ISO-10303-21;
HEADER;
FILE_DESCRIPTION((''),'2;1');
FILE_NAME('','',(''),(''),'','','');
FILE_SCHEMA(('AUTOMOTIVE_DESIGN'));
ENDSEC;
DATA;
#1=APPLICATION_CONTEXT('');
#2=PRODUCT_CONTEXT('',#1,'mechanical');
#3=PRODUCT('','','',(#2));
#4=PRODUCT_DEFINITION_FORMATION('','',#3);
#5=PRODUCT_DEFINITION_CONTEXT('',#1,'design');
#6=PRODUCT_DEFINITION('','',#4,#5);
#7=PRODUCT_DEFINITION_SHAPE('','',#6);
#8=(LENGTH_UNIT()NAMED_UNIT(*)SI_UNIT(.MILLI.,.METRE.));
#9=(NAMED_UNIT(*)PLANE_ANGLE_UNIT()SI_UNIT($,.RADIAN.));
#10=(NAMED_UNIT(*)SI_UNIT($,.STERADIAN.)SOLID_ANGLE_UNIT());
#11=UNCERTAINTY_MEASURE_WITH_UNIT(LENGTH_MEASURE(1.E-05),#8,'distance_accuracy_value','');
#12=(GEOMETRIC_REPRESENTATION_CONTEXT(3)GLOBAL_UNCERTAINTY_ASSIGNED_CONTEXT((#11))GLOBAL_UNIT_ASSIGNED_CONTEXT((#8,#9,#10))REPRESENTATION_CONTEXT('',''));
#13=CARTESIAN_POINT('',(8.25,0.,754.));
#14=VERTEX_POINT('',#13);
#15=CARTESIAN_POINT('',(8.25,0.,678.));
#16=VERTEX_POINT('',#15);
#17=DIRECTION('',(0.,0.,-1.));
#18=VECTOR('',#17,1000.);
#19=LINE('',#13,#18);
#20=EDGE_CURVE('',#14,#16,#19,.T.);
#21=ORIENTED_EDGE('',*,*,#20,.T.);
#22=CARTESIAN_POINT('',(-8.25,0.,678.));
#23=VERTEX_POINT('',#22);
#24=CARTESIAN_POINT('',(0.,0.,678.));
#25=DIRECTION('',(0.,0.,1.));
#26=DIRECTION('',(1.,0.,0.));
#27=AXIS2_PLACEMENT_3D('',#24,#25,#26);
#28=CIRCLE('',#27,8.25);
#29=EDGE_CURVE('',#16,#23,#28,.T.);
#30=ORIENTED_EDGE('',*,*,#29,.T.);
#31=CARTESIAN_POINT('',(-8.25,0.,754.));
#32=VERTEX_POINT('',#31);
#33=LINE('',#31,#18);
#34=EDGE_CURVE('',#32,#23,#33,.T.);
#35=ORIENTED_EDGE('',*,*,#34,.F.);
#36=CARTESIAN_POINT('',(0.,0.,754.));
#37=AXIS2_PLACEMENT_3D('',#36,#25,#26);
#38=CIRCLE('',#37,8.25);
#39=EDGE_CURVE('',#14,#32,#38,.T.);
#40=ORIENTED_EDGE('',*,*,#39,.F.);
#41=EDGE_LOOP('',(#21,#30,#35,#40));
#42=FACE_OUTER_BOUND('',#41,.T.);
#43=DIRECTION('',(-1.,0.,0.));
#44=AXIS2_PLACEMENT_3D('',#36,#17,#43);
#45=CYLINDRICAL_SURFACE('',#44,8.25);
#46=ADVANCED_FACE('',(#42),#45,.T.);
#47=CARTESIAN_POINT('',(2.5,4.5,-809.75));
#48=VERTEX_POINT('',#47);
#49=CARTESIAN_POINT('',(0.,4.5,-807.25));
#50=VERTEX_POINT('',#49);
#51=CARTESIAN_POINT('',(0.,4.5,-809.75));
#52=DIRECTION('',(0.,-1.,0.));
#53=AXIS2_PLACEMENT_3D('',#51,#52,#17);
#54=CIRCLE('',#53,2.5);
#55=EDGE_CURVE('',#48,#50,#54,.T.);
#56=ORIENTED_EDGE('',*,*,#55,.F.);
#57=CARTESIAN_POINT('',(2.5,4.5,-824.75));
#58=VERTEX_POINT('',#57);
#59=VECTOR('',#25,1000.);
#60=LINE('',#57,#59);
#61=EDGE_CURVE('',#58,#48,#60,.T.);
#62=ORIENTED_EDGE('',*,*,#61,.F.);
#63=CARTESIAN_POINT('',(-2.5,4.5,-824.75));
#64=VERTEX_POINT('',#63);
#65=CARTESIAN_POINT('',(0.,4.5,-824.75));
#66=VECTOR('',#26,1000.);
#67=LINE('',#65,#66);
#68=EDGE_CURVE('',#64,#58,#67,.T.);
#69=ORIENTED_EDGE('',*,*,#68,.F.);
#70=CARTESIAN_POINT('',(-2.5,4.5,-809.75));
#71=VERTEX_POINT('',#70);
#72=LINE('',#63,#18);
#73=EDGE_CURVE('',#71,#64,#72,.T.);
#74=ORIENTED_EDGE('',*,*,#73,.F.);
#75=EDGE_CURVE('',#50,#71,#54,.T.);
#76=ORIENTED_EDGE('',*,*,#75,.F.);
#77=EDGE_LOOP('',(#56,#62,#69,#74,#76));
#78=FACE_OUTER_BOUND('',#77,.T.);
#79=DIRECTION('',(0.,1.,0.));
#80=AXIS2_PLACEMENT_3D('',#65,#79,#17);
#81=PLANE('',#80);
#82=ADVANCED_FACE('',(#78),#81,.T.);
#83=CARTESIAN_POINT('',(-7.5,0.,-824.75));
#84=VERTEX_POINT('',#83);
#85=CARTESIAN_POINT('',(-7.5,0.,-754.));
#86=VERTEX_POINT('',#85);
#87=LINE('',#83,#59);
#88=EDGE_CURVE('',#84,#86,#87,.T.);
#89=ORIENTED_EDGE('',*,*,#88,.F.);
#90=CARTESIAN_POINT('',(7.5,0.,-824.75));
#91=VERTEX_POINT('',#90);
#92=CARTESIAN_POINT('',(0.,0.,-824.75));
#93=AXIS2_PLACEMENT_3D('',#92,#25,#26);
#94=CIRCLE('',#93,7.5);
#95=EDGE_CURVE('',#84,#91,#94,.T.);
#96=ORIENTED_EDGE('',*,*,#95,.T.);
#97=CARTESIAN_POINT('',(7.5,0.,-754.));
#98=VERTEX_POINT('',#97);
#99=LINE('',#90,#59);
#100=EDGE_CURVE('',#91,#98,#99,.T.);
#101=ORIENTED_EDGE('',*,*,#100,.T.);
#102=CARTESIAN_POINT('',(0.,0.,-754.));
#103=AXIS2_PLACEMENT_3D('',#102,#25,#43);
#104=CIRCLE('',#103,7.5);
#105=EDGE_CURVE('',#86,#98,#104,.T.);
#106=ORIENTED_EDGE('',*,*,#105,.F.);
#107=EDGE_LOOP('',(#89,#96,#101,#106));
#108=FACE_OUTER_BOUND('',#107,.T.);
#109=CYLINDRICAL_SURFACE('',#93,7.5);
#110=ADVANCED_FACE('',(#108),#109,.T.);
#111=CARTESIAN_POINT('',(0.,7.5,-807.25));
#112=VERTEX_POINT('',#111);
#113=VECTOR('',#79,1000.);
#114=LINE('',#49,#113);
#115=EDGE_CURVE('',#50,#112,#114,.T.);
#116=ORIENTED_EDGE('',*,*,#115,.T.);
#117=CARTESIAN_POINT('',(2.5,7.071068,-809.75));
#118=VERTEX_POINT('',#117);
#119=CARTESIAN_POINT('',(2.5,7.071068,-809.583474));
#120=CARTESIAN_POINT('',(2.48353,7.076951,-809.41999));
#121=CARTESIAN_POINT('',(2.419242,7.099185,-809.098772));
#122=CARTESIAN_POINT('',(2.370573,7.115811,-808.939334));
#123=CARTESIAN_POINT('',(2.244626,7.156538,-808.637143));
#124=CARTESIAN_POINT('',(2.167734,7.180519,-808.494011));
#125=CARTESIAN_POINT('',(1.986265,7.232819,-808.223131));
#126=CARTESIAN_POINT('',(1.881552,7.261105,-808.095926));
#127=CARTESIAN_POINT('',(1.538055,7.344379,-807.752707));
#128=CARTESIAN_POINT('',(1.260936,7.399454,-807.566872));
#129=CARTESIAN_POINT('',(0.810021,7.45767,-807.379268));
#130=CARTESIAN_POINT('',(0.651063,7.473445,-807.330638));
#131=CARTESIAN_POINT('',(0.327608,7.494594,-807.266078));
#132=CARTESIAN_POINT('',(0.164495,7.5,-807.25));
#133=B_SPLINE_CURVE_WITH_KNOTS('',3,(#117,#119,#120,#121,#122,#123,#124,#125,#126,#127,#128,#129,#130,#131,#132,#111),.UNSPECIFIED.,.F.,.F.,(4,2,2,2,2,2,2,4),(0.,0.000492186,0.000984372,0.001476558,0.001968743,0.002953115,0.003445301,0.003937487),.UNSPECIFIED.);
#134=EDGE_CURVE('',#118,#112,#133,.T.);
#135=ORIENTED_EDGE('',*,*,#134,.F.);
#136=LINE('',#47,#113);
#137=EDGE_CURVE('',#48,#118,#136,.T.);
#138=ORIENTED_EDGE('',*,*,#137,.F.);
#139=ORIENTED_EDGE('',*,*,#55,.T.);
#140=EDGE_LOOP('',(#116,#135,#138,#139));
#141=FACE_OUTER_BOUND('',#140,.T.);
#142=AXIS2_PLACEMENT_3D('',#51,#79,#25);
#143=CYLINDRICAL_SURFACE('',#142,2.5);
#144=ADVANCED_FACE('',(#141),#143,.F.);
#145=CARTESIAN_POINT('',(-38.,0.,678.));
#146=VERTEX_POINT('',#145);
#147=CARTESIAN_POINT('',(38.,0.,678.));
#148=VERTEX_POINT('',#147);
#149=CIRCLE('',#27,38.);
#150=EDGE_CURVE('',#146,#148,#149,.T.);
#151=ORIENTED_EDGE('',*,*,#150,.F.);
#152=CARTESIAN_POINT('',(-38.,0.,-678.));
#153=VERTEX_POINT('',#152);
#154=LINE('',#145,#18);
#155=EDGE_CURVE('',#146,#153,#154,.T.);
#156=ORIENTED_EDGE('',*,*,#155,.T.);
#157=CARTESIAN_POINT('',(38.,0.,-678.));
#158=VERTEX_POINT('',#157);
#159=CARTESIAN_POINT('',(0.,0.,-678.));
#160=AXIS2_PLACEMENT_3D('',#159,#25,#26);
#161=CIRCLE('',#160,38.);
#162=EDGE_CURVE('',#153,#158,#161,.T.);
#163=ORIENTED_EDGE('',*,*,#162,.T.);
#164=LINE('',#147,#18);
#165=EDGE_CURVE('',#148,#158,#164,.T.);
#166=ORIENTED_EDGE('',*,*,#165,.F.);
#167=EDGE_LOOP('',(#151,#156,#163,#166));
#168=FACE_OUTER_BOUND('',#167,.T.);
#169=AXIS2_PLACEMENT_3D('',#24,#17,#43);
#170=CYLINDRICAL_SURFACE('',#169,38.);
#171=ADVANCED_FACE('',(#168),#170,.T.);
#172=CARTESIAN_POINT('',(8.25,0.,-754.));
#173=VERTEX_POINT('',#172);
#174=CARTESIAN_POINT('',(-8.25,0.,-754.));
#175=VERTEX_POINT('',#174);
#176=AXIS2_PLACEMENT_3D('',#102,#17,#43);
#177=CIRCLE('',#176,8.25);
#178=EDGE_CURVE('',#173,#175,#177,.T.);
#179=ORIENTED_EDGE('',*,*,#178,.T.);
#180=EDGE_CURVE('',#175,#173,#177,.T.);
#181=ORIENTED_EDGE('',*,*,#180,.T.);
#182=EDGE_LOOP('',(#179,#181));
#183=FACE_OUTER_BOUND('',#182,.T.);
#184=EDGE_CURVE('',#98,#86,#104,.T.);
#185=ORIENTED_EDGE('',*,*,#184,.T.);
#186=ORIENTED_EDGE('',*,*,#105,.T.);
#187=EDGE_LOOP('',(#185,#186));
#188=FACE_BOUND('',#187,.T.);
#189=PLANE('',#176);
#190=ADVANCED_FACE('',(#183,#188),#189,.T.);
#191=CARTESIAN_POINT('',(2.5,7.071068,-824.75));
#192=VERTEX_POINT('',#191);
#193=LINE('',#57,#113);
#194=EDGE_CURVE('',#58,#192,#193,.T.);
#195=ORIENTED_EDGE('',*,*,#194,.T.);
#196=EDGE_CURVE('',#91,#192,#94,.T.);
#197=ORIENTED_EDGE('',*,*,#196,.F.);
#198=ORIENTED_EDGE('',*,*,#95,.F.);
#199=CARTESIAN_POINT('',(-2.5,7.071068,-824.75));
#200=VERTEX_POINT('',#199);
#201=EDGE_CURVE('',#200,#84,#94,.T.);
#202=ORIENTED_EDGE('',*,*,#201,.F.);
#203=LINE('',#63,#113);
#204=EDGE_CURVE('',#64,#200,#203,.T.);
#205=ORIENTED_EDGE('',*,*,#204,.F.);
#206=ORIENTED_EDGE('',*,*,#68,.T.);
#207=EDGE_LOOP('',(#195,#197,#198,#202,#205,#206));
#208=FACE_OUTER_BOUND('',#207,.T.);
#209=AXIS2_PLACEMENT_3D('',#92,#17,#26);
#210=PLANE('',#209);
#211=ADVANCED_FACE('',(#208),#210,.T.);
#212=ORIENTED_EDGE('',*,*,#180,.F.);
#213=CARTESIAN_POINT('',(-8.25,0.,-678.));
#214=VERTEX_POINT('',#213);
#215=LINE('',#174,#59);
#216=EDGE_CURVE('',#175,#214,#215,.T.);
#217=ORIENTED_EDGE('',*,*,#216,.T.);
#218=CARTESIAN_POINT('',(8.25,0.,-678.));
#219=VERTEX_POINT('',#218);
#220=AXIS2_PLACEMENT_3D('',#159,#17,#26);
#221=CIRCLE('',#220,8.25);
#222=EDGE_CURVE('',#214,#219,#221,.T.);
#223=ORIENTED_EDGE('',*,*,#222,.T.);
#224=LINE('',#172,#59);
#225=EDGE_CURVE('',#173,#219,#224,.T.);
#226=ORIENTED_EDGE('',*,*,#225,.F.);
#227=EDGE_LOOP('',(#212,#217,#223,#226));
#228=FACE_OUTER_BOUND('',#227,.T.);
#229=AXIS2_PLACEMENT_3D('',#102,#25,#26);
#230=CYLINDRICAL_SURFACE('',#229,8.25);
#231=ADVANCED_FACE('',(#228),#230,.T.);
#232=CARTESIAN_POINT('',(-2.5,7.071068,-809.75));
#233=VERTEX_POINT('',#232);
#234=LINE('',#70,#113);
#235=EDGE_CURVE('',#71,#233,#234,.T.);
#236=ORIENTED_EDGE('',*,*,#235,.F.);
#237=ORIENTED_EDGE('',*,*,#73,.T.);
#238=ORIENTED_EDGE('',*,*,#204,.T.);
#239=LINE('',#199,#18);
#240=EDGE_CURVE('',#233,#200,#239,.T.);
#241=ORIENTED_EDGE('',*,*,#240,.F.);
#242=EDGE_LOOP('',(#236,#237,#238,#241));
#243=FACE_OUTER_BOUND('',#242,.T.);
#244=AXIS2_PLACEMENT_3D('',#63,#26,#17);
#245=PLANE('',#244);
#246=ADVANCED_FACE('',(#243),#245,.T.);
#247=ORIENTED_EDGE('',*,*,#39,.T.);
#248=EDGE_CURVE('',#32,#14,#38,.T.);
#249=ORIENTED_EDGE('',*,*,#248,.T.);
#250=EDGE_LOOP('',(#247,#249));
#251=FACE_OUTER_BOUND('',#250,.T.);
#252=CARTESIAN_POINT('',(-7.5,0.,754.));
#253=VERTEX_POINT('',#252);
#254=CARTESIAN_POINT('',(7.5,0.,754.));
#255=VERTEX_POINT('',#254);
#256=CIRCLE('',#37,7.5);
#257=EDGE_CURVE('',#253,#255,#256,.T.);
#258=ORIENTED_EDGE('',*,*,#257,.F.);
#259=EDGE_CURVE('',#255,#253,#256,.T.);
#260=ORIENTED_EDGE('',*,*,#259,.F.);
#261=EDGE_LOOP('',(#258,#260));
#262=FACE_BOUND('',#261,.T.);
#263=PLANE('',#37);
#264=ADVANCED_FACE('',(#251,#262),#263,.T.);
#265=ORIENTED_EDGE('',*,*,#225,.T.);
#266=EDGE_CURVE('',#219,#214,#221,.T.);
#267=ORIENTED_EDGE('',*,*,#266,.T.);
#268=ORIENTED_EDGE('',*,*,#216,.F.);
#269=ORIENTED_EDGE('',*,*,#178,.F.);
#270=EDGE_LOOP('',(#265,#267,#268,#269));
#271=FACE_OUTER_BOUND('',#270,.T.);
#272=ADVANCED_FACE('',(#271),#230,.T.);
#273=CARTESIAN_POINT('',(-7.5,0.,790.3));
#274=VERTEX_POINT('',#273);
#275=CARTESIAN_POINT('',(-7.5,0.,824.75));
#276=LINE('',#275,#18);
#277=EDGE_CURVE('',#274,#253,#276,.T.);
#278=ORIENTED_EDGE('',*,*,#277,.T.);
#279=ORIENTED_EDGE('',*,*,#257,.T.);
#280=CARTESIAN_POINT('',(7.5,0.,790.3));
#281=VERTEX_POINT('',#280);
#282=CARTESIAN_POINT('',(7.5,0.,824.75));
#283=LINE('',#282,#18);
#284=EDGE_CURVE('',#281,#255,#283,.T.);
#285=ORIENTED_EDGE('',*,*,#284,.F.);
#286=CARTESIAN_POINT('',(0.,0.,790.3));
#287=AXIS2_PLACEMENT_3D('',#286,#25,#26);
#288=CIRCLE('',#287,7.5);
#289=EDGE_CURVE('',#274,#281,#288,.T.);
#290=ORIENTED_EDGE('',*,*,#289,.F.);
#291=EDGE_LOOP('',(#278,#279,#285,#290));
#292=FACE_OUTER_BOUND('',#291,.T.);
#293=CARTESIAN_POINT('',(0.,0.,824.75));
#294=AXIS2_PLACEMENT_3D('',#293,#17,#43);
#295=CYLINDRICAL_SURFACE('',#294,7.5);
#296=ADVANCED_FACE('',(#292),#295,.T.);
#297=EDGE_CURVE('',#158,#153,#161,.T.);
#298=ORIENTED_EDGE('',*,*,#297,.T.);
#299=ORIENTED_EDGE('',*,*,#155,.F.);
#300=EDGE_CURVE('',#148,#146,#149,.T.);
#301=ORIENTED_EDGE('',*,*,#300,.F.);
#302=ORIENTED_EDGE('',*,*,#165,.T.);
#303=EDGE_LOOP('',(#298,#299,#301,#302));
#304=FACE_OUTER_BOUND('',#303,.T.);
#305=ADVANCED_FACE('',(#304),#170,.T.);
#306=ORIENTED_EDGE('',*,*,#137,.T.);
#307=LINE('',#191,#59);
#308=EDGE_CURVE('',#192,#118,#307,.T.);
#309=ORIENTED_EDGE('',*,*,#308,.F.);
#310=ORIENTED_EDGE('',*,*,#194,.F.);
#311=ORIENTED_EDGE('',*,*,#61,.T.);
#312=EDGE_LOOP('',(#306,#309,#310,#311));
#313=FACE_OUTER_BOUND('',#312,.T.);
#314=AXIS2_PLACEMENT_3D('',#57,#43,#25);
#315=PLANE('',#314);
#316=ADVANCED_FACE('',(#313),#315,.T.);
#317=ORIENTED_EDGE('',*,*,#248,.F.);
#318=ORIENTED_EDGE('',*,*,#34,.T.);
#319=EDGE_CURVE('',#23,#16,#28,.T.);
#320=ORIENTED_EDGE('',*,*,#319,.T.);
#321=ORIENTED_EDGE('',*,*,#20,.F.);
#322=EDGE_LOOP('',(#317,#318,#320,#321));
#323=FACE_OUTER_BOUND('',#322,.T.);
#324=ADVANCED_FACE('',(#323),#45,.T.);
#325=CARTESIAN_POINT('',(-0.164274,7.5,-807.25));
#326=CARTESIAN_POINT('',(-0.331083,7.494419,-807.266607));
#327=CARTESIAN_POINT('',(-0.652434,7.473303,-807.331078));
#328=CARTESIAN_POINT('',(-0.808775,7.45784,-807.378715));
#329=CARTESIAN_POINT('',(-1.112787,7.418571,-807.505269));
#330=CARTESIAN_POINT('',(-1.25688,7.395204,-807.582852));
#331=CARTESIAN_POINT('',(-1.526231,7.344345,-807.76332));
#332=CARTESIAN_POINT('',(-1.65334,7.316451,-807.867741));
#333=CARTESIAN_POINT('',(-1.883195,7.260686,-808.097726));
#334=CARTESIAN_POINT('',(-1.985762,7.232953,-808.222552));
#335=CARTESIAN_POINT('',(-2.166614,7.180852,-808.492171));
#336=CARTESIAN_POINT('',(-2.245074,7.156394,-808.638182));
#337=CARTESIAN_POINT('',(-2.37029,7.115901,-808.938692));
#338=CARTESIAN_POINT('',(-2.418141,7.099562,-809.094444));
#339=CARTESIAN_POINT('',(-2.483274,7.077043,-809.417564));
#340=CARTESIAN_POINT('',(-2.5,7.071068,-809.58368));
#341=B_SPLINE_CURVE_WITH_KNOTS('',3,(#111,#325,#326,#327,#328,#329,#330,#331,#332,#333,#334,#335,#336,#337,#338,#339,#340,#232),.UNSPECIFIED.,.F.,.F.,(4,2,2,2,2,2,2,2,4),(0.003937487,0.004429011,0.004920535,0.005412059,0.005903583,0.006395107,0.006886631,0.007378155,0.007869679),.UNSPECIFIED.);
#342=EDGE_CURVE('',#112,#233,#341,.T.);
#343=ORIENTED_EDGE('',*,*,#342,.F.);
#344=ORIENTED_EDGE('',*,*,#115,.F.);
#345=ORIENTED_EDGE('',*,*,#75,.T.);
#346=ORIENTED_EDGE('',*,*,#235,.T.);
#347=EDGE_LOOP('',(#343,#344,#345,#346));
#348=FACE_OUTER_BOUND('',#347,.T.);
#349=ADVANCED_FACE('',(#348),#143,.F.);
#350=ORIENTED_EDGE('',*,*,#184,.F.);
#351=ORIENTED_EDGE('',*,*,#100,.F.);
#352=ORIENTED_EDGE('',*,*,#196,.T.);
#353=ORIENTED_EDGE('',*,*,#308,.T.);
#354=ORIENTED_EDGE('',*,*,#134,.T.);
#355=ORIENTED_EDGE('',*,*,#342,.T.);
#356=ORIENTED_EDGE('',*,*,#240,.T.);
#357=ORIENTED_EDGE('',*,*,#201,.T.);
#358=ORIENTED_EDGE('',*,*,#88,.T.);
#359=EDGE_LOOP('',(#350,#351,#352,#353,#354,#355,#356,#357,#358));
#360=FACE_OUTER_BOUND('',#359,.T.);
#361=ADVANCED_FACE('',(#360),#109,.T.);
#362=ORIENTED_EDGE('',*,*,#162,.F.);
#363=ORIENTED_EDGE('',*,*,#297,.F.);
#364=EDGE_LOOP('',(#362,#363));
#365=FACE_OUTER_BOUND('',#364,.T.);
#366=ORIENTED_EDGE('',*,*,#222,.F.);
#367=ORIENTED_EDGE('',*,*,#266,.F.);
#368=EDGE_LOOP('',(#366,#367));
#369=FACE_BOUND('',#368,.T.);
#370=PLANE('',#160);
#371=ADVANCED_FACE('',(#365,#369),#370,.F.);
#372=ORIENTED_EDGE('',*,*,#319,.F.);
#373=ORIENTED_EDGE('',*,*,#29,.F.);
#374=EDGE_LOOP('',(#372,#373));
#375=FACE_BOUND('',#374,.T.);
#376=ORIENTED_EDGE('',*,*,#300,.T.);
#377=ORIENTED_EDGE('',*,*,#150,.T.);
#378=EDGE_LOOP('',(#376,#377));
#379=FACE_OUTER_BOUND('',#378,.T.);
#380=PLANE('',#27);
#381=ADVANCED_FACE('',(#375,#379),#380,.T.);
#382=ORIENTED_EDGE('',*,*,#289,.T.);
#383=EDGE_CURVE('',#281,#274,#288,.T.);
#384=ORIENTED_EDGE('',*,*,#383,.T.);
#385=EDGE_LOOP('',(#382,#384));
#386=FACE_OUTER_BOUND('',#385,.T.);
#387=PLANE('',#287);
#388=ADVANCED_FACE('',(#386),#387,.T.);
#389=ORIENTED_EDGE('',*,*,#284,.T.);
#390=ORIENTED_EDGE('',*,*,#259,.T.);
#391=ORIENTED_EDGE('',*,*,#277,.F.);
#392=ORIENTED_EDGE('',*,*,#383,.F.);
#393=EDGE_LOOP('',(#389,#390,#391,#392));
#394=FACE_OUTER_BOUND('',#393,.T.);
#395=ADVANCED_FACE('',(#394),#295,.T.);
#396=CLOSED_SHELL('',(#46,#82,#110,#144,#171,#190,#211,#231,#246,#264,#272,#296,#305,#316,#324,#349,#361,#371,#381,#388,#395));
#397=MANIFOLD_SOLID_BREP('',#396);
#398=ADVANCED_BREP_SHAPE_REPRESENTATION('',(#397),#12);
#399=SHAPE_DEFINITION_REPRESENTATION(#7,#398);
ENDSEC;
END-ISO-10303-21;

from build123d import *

# Parameters (mm, degrees)
SKETCH_1_R          = 38
EXTRUDE_1_DEPTH     = 678
SKETCH_2_R          = 7.5
EXTRUDE_2_DEPTH     = 146.75
SKETCH_3_R          = 8.25
EXTRUDE_4_DEPTH     = 76
EXTRUDE_START       = 76
SKETCH_4_R          = 8.25
EXTRUDE_5_DEPTH     = 76
CUT_EXTRUDE_START   = 7.5
CUT_EXTRUDE_2_DEPTH = 3
SKETCH_9_R          = 14.996083322
CUT_EXTRUDE_4_DEPTH = 34.45


with BuildPart() as part:
    # 草图1 → 凸台-拉伸1 (new, symmetric)
    with BuildSketch(Plane.XY):
        Circle(SKETCH_1_R)
    extrude(amount=EXTRUDE_1_DEPTH, both=True)

    # 草图2 → 凸台-拉伸2 (add, symmetric)
    with BuildSketch(Plane.XY.offset(678)):
        with Locations(Location((0, 0, 0), (0, 0, 180))):
            Circle(SKETCH_2_R)
    extrude_2 = extrude(amount=EXTRUDE_2_DEPTH, both=True)

    # 镜向1: 凸台-拉伸2 across plane
    add(extrude_2.mirror(Plane.XY))

    # 草图3 → 凸台-拉伸4 (add)
    with BuildSketch(Plane.XY.offset(678)):
        Circle(SKETCH_3_R)
    extrude(amount=EXTRUDE_4_DEPTH)

    # 草图4 → 凸台-拉伸5 (add)
    with BuildSketch(Plane(origin=(0, 0, -678), x_dir=(-1, 0, 0), z_dir=(0, 0, -1)).offset(EXTRUDE_START)):
        with Locations(Location((0, 0, 0), (0, 0, 180))):
            Circle(SKETCH_4_R)
    extrude(amount=-EXTRUDE_5_DEPTH)

    # 草图6 → 切除-拉伸2 (cut)
    with BuildSketch(Plane(origin=(0, 0, 0), x_dir=(1, 0, 0), z_dir=(0, 1, 0)).offset(CUT_EXTRUDE_START)):
        with BuildLine():
            Line((-2.5, -824.75), (-2.5, -809.75))
            ThreePointArc((-2.5, -809.75), (0, -807.25), (2.5, -809.75))
            Line((2.5, -809.75), (2.5, -824.75))
            ThreePointArc((2.5, -824.75), (0, -827.25), (-2.5, -824.75))
        make_face()
    cut_extrude_2 = extrude(amount=-CUT_EXTRUDE_2_DEPTH, mode=Mode.SUBTRACT)

    # 镜向2: 切除-拉伸2 across plane
    add(cut_extrude_2.mirror(Plane.XY), mode=Mode.SUBTRACT)

    # 草图9 → 切除-拉伸4 (cut)
    with BuildSketch(Plane.XY.offset(824.75)):
        Circle(SKETCH_9_R)
    extrude(amount=-CUT_EXTRUDE_4_DEPTH, mode=Mode.SUBTRACT)


solid = part.part
